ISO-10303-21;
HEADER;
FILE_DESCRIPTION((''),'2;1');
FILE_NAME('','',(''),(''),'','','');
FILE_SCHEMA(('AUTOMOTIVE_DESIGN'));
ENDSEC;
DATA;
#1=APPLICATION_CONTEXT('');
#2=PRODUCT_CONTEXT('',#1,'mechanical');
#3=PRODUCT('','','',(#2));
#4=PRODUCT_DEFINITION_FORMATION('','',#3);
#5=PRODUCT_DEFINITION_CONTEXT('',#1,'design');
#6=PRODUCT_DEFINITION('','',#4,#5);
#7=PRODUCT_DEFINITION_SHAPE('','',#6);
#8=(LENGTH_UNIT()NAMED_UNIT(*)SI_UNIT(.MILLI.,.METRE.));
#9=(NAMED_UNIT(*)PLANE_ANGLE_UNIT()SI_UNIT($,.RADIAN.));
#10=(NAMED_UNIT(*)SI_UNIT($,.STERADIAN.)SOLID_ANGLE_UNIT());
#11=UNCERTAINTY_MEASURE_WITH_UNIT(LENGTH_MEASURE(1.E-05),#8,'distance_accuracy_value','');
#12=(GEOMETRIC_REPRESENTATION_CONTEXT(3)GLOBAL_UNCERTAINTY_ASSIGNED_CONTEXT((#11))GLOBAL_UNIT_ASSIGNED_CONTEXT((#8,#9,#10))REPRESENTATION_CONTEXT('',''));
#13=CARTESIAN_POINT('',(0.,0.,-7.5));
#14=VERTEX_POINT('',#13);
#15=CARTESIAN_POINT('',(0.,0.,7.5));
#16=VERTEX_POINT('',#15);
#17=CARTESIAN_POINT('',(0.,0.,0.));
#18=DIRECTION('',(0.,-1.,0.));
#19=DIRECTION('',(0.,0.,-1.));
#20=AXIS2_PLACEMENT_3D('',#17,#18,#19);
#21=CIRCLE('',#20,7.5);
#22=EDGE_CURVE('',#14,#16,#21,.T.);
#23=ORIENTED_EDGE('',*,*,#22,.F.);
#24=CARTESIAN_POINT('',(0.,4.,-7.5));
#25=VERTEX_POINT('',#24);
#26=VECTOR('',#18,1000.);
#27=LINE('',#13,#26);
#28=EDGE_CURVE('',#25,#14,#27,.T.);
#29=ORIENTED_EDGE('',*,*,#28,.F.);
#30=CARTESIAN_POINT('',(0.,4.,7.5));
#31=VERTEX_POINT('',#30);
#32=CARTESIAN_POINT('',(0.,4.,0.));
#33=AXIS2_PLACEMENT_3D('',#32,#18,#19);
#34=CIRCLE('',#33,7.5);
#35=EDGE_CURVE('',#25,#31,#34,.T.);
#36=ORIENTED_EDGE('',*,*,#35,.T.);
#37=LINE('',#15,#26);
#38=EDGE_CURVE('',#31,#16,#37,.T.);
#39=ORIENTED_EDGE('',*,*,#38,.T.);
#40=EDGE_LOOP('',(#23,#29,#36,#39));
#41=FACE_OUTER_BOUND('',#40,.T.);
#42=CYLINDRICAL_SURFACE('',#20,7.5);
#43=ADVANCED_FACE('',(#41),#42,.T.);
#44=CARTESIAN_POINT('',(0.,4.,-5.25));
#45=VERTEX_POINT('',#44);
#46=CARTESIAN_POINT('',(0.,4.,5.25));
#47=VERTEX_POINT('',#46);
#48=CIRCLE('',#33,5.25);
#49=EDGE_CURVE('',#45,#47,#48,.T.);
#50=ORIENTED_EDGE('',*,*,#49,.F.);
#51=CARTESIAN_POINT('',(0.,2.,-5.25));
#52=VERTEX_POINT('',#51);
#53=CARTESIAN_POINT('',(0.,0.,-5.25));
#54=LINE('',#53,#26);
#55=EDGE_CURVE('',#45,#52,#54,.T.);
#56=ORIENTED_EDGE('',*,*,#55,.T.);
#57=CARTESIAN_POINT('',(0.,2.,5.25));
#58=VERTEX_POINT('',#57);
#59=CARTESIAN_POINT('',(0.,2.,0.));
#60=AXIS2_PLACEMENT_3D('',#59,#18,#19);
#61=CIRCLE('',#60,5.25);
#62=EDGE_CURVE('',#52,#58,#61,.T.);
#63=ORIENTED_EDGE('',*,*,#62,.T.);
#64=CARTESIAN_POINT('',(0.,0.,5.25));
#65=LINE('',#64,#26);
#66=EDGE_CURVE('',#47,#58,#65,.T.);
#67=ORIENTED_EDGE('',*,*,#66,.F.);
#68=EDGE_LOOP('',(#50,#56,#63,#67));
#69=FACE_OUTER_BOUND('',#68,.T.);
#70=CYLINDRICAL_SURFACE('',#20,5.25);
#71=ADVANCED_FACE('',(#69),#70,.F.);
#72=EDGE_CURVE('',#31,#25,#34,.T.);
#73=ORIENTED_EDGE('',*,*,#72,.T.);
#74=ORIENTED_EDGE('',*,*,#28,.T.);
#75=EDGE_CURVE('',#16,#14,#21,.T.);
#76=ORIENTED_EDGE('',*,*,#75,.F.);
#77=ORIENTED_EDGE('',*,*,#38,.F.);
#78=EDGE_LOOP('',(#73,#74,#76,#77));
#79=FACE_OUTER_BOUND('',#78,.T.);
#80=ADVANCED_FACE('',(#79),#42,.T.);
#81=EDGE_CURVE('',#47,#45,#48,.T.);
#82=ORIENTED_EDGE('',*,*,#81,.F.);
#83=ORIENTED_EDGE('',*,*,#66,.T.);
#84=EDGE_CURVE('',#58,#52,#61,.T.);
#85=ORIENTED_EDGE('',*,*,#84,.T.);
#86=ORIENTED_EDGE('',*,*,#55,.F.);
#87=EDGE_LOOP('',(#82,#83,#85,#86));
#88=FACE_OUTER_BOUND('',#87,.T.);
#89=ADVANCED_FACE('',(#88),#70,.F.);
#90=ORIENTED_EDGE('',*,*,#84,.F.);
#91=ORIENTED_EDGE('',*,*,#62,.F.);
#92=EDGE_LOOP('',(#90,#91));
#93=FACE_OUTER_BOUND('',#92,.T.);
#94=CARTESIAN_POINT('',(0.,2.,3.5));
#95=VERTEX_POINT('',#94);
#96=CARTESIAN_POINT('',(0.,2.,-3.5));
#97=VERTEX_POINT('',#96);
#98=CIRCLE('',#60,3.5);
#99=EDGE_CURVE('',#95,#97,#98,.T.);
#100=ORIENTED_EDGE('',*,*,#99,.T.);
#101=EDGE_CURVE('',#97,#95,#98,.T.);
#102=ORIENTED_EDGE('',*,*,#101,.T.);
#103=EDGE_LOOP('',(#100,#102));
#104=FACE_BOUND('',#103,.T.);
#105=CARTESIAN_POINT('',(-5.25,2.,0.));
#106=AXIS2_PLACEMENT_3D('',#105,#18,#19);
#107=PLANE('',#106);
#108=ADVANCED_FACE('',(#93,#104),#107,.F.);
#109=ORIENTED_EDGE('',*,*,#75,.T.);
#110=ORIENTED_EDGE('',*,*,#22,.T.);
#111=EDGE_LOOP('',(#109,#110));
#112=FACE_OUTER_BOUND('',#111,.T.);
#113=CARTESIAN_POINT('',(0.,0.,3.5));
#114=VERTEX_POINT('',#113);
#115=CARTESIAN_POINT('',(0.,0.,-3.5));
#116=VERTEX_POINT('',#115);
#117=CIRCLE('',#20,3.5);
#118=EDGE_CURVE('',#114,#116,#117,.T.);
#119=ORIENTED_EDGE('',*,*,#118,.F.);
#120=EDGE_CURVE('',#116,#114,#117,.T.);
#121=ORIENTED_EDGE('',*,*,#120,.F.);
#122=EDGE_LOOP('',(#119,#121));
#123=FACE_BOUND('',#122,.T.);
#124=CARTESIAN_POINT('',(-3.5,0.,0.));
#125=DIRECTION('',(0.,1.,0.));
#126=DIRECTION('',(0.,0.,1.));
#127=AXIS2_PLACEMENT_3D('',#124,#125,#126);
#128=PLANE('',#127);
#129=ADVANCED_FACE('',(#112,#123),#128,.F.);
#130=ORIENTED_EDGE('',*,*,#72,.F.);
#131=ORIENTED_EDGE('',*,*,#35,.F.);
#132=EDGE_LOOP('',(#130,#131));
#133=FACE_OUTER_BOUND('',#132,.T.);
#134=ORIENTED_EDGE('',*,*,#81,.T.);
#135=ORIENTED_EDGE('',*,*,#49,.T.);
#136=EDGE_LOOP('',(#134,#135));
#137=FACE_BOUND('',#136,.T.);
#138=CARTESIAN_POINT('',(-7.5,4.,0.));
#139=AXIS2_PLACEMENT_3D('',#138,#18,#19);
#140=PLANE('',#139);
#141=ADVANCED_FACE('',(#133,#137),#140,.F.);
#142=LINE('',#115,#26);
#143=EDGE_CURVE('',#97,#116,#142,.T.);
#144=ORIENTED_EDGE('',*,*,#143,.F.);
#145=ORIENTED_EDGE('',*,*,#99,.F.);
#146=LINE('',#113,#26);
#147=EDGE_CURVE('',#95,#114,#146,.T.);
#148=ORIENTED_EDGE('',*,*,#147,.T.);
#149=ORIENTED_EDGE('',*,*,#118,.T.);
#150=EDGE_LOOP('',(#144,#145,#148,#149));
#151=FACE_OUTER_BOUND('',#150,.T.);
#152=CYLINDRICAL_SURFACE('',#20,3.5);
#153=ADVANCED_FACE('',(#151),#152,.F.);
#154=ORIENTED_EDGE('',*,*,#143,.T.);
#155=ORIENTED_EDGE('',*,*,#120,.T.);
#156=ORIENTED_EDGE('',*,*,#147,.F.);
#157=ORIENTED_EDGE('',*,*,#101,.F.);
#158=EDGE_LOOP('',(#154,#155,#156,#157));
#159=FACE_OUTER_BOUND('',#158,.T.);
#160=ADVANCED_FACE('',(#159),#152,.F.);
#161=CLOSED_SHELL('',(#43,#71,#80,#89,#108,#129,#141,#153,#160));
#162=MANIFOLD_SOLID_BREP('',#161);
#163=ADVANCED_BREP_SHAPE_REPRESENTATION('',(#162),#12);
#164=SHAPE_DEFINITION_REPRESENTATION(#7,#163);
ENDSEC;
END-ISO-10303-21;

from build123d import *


with BuildPart() as part:
    # Sketch1 → Revolve1 (revolve)
    with BuildSketch(Plane.XY, mode=Mode.PRIVATE) as revolve1_sk:
        Polygon((-3.5, 0), (-7.5, 0), (-7.5, 4), (-5.25, 4), (-5.25, 2), (-3.5, 2), align=None)
    revolve(revolve1_sk.sketch.rotate(Axis((0, 0, 0), (0, 1, 0)), 270), axis=Axis((0, 0, 0), (0, 1, 0)))


solid = part.part
